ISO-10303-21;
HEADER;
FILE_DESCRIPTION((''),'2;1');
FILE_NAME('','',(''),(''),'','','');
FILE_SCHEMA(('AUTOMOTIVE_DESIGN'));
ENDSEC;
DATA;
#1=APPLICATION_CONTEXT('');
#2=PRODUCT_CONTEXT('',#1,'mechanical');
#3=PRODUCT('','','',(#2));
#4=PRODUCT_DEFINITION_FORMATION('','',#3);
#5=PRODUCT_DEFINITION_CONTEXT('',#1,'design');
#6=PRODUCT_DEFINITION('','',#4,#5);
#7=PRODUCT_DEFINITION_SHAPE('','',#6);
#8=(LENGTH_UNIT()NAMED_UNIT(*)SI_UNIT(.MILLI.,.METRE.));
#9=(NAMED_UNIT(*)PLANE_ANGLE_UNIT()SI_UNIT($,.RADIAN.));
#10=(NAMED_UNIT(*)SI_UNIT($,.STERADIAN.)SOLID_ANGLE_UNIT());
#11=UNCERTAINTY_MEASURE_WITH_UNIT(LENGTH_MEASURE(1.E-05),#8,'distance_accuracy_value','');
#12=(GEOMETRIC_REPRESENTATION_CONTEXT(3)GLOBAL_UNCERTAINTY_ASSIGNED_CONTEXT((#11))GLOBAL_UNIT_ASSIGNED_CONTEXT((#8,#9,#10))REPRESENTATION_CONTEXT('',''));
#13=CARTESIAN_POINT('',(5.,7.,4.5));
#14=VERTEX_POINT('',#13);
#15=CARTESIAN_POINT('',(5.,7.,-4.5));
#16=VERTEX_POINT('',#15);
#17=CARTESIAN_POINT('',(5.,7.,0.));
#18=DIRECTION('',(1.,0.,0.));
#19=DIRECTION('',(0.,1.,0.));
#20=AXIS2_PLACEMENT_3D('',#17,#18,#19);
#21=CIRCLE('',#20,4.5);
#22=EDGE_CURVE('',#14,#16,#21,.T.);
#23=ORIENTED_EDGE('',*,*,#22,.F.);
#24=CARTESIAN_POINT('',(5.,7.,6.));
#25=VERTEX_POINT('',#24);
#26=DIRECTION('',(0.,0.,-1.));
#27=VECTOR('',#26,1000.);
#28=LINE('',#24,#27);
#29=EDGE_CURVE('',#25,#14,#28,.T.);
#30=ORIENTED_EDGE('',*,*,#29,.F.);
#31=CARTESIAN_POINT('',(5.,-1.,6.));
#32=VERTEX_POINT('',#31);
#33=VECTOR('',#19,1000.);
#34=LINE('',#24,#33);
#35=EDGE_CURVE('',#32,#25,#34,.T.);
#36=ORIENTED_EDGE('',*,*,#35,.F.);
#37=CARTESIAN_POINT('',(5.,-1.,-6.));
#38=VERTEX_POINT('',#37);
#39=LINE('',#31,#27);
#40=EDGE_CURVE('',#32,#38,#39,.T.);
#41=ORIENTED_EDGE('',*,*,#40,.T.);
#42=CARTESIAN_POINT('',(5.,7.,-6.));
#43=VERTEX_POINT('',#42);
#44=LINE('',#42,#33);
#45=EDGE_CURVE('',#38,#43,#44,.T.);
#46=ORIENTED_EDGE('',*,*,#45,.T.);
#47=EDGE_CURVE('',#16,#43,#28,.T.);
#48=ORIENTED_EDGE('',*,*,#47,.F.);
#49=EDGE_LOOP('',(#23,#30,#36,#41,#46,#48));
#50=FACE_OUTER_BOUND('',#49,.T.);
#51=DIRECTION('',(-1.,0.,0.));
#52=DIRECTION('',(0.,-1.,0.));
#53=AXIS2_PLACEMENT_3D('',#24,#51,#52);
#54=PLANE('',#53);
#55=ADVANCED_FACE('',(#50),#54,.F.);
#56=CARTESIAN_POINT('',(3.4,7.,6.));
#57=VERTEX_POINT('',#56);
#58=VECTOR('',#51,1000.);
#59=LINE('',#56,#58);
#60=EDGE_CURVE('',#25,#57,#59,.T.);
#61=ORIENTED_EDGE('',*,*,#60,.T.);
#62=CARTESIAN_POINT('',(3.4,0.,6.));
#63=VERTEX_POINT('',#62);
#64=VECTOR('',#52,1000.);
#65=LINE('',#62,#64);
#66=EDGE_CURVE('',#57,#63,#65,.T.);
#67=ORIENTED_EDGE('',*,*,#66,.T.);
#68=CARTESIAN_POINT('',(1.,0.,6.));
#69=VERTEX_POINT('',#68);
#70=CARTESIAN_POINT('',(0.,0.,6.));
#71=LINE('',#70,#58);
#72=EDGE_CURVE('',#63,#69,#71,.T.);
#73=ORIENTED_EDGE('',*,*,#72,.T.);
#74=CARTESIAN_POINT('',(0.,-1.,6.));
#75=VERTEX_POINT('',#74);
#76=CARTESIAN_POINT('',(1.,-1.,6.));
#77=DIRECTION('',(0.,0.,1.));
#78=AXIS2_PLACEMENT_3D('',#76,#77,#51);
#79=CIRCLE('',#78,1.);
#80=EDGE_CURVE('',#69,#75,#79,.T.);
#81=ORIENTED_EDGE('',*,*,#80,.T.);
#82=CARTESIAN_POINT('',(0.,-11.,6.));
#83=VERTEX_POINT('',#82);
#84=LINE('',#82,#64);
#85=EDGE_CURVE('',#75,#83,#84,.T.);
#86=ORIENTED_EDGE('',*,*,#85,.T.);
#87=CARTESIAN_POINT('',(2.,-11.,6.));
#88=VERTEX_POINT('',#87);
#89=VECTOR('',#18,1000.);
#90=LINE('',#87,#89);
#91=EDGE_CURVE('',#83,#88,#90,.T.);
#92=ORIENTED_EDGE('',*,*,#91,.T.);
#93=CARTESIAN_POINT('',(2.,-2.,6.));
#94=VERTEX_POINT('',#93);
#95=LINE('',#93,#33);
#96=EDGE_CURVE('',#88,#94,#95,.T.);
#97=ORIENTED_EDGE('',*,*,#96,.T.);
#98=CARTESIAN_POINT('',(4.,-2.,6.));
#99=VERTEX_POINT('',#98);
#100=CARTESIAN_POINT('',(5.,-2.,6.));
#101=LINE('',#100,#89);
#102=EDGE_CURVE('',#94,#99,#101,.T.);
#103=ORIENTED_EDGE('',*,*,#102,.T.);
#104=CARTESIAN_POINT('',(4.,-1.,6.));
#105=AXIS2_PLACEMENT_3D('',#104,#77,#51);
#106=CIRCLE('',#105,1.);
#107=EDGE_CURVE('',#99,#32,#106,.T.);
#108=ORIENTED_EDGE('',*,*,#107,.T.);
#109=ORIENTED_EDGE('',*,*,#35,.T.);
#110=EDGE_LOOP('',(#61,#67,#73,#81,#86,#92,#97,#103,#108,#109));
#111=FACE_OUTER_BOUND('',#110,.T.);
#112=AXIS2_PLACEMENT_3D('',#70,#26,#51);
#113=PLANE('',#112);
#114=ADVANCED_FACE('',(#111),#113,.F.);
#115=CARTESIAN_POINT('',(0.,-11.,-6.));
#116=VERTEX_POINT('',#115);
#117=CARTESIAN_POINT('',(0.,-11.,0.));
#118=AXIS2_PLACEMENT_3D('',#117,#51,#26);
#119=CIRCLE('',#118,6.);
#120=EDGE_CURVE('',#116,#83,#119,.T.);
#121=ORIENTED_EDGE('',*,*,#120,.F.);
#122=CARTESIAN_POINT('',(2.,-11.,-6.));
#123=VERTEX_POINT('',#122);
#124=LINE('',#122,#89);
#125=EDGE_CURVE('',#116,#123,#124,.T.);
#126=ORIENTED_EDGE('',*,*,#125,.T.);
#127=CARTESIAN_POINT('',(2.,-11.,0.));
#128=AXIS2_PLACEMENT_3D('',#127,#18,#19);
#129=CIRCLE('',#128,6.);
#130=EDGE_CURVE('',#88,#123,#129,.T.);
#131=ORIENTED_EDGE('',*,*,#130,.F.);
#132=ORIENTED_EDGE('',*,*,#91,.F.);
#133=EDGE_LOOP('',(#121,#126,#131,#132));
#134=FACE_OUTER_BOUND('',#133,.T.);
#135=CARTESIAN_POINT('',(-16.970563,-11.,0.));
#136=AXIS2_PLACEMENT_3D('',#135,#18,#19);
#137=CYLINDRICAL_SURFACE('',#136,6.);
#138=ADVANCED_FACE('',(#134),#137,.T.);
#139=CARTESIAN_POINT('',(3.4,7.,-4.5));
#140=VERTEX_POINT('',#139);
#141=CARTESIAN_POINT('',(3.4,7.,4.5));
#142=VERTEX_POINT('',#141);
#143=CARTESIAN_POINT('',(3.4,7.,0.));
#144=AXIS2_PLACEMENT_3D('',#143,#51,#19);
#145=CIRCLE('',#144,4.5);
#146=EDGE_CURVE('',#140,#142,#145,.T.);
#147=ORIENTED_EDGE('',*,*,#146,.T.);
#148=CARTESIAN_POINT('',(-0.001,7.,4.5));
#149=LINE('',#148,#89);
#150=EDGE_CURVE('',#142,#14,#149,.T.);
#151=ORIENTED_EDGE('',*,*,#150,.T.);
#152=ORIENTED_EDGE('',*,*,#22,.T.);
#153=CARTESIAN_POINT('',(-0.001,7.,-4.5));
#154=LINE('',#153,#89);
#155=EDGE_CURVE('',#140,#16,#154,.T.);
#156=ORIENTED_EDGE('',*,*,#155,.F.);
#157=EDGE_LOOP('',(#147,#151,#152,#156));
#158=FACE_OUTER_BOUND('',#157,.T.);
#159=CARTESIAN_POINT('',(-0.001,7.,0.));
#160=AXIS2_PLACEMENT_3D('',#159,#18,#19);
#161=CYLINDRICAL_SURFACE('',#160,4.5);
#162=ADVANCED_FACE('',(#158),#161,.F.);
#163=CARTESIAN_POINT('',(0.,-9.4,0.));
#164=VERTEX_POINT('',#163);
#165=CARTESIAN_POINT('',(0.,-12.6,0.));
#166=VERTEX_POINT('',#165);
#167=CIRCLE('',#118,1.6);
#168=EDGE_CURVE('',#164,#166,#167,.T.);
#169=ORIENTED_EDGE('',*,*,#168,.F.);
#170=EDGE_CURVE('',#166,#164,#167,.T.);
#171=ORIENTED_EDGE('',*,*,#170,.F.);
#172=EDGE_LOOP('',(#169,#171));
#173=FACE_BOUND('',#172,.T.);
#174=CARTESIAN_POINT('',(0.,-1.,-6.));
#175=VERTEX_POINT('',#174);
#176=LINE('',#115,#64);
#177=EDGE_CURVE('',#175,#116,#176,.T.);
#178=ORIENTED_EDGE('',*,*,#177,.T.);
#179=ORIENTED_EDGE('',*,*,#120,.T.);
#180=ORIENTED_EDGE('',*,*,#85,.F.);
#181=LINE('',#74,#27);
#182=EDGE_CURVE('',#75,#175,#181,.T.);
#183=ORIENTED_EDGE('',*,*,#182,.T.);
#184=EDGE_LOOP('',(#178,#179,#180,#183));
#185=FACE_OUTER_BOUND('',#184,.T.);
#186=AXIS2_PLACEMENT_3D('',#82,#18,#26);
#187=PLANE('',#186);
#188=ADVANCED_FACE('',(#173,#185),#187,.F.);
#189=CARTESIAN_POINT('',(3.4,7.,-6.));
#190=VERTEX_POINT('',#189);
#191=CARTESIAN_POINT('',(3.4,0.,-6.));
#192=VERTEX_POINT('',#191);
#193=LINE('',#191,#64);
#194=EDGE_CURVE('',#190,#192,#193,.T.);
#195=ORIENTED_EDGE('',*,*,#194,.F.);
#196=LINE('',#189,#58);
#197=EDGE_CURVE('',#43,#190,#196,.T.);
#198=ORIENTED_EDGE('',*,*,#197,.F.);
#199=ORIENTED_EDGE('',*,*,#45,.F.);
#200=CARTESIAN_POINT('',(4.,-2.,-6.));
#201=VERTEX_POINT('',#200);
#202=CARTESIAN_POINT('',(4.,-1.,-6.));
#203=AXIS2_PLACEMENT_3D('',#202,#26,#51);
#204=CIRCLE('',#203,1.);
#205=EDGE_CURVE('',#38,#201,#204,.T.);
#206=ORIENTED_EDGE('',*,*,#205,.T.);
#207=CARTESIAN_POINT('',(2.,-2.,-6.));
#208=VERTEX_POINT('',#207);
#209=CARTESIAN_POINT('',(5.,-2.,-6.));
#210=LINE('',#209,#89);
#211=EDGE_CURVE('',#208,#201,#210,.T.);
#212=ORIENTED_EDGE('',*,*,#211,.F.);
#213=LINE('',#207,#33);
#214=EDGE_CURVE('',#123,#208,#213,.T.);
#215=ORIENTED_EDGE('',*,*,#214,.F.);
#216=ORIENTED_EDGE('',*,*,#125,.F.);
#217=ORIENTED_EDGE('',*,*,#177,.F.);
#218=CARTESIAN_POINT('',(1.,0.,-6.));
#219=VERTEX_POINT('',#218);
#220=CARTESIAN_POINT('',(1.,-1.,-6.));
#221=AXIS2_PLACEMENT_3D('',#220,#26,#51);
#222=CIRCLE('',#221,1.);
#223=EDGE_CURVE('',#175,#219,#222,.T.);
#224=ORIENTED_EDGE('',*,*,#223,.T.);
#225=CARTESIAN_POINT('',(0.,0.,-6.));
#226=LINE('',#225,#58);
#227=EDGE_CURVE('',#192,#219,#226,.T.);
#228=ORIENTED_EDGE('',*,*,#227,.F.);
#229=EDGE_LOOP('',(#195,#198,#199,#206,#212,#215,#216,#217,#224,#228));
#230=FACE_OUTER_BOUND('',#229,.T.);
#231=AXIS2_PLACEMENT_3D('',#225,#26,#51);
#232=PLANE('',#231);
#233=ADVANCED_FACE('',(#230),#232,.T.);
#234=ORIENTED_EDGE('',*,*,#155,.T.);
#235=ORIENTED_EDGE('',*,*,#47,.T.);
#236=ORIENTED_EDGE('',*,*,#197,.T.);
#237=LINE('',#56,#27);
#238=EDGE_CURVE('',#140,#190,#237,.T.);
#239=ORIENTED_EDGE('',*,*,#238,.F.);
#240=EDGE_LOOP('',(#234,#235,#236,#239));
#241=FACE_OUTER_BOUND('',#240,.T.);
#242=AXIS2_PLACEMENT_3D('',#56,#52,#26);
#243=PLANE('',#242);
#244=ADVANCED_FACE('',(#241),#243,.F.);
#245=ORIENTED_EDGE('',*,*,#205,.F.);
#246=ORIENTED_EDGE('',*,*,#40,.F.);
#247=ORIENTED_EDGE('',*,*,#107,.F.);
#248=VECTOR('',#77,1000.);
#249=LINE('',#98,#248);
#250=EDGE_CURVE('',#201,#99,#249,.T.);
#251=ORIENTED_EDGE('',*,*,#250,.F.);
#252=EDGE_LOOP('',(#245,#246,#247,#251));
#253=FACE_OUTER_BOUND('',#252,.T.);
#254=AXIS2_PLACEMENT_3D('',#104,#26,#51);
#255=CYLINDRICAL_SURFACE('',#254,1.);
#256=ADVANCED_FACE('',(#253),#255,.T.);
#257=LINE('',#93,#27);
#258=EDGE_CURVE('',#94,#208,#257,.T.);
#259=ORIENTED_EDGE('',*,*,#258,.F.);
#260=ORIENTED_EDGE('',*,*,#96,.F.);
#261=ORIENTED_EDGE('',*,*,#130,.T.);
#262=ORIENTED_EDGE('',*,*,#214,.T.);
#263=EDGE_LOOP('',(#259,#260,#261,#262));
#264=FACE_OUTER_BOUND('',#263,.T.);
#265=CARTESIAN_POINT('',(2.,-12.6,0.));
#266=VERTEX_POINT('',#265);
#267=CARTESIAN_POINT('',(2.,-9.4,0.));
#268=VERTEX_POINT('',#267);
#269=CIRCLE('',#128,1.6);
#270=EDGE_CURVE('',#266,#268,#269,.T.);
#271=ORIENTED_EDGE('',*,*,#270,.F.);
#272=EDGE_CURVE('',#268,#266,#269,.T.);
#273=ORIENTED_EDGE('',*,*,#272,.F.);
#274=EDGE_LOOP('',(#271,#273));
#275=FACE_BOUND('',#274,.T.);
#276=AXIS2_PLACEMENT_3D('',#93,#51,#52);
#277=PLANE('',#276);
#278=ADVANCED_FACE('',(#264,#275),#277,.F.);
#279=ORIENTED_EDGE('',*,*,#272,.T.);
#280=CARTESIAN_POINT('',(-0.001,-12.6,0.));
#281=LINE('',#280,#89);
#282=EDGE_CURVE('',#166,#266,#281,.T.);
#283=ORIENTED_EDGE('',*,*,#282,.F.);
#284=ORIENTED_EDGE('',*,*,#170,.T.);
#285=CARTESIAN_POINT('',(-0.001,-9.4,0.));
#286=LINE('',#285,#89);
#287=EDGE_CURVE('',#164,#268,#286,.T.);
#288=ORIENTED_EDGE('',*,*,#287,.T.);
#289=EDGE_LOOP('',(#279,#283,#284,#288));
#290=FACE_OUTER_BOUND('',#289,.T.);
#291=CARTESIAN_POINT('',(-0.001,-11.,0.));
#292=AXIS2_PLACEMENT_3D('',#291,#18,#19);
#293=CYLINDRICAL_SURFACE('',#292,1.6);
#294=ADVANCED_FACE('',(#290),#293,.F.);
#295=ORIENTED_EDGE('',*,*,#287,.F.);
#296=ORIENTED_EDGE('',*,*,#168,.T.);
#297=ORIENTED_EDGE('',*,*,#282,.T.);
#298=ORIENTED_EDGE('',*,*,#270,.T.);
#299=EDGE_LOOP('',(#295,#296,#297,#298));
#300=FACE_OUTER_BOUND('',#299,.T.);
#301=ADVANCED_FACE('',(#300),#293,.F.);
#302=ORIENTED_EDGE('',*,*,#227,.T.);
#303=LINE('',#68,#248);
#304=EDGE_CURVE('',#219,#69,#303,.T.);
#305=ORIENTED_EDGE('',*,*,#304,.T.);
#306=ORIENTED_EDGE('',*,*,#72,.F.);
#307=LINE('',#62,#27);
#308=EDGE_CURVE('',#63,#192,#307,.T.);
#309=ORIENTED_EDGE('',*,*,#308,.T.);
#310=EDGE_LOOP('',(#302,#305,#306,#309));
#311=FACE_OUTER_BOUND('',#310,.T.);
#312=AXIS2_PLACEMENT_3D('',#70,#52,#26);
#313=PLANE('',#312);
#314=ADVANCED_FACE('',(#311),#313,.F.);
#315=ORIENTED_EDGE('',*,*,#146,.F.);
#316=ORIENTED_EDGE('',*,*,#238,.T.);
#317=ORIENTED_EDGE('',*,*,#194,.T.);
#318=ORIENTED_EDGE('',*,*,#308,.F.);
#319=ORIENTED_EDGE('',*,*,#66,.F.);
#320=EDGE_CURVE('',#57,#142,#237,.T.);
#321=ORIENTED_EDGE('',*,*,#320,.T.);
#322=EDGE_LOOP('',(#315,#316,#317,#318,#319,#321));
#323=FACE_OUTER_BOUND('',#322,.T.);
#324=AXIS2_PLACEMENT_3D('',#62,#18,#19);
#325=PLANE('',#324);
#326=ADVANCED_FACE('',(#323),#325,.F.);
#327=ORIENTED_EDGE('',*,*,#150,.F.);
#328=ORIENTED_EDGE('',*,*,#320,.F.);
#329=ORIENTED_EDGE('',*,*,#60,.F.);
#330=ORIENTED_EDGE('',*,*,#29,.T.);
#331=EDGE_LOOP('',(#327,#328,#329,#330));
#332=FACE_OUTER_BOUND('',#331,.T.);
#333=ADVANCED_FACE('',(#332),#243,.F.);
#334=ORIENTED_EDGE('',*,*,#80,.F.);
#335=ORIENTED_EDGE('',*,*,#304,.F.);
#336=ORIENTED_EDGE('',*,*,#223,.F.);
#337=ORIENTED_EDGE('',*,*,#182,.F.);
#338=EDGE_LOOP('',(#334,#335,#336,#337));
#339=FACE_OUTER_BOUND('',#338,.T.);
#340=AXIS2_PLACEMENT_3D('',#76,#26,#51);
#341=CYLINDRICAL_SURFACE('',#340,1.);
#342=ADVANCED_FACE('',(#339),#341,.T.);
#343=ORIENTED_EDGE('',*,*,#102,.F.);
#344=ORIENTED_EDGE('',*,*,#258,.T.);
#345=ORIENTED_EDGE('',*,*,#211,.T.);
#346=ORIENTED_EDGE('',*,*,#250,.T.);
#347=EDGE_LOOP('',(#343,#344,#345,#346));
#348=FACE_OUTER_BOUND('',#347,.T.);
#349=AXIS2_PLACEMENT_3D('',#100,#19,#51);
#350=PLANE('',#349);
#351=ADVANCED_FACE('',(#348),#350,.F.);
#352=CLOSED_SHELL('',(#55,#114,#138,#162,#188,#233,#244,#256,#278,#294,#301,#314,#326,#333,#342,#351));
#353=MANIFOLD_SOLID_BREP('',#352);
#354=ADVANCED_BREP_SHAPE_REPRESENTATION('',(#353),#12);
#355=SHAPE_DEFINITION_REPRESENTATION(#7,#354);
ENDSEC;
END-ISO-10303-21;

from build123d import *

# Parameters (mm, degrees)
CLIP_BODY_DEPTH      = 6
ROUNDED_TAB_SKETCH_R = 6
ROUNDED_TAB_DEPTH    = 2
SADDLE_CUT_REACH     = 20.708
PIVOT_HOLE_3_2_REACH = 20.276
PIVOT_HOLE_SKETCH_R  = 1.6
EDGE_FILLETS_R1_R    = 1


with BuildPart() as part:
    # Clip Profile Sketch → Clip Body (new, symmetric)
    with BuildSketch(Plane.XY):
        Polygon((0, -11), (0, 0), (3.4, 0), (3.4, 7), (5, 7), (5, -2), (2, -2), (2, -11), align=None)
    extrude(amount=CLIP_BODY_DEPTH, both=True)

    # Rounded Tab Sketch → Rounded Tab (add)
    with BuildSketch(Plane(origin=(2, 0, 0), x_dir=(0, 0, -1), z_dir=(1, 0, 0))):
        with Locations((0, -11)):
            Circle(ROUNDED_TAB_SKETCH_R)
    extrude(amount=-ROUNDED_TAB_DEPTH)

    # Saddle Cut Sketch → Saddle Cut (cut, up to next)
    with BuildSketch(Plane(origin=(5, 0, 0), x_dir=(0, 0, -1), z_dir=(1, 0, 0)), mode=Mode.PRIVATE) as saddle_cut_sk1:
        with BuildLine():
            Line((-4.5, 7), (4.5, 7))
            ThreePointArc((4.5, 7), (0, 2.5), (-4.5, 7))
        make_face()
    saddle_cut_tool1 = extrude(saddle_cut_sk1.sketch, amount=-SADDLE_CUT_REACH, mode=Mode.PRIVATE) & part.part
    add(saddle_cut_tool1.solids().sort_by_distance((5, 5.090141, 0))[0], mode=Mode.SUBTRACT)

    # Pivot Hole Sketch → Pivot Hole Ø3.2 (cut, up to next)
    with BuildSketch(Plane(origin=(2, 0, 0), x_dir=(0, 0, -1), z_dir=(1, 0, 0)), mode=Mode.PRIVATE) as pivot_hole_3_2_sk1:
        with Locations(Location((0, -11, 0), (0, 0, 90))):
            Circle(PIVOT_HOLE_SKETCH_R)
    pivot_hole_3_2_tool1 = extrude(pivot_hole_3_2_sk1.sketch, amount=-PIVOT_HOLE_3_2_REACH, mode=Mode.PRIVATE) & part.part
    add(pivot_hole_3_2_tool1.solids().sort_by_distance((2, -11, 0))[0], mode=Mode.SUBTRACT)

    # Edge Fillets R1
    edge_fillets_r1_edges = [part.edges().sort_by_distance(p)[0] for p in [
        (0, 0, 0),
        (5, -2, 0),
    ]]
    fillet(edge_fillets_r1_edges, radius=EDGE_FILLETS_R1_R)


solid = part.part
